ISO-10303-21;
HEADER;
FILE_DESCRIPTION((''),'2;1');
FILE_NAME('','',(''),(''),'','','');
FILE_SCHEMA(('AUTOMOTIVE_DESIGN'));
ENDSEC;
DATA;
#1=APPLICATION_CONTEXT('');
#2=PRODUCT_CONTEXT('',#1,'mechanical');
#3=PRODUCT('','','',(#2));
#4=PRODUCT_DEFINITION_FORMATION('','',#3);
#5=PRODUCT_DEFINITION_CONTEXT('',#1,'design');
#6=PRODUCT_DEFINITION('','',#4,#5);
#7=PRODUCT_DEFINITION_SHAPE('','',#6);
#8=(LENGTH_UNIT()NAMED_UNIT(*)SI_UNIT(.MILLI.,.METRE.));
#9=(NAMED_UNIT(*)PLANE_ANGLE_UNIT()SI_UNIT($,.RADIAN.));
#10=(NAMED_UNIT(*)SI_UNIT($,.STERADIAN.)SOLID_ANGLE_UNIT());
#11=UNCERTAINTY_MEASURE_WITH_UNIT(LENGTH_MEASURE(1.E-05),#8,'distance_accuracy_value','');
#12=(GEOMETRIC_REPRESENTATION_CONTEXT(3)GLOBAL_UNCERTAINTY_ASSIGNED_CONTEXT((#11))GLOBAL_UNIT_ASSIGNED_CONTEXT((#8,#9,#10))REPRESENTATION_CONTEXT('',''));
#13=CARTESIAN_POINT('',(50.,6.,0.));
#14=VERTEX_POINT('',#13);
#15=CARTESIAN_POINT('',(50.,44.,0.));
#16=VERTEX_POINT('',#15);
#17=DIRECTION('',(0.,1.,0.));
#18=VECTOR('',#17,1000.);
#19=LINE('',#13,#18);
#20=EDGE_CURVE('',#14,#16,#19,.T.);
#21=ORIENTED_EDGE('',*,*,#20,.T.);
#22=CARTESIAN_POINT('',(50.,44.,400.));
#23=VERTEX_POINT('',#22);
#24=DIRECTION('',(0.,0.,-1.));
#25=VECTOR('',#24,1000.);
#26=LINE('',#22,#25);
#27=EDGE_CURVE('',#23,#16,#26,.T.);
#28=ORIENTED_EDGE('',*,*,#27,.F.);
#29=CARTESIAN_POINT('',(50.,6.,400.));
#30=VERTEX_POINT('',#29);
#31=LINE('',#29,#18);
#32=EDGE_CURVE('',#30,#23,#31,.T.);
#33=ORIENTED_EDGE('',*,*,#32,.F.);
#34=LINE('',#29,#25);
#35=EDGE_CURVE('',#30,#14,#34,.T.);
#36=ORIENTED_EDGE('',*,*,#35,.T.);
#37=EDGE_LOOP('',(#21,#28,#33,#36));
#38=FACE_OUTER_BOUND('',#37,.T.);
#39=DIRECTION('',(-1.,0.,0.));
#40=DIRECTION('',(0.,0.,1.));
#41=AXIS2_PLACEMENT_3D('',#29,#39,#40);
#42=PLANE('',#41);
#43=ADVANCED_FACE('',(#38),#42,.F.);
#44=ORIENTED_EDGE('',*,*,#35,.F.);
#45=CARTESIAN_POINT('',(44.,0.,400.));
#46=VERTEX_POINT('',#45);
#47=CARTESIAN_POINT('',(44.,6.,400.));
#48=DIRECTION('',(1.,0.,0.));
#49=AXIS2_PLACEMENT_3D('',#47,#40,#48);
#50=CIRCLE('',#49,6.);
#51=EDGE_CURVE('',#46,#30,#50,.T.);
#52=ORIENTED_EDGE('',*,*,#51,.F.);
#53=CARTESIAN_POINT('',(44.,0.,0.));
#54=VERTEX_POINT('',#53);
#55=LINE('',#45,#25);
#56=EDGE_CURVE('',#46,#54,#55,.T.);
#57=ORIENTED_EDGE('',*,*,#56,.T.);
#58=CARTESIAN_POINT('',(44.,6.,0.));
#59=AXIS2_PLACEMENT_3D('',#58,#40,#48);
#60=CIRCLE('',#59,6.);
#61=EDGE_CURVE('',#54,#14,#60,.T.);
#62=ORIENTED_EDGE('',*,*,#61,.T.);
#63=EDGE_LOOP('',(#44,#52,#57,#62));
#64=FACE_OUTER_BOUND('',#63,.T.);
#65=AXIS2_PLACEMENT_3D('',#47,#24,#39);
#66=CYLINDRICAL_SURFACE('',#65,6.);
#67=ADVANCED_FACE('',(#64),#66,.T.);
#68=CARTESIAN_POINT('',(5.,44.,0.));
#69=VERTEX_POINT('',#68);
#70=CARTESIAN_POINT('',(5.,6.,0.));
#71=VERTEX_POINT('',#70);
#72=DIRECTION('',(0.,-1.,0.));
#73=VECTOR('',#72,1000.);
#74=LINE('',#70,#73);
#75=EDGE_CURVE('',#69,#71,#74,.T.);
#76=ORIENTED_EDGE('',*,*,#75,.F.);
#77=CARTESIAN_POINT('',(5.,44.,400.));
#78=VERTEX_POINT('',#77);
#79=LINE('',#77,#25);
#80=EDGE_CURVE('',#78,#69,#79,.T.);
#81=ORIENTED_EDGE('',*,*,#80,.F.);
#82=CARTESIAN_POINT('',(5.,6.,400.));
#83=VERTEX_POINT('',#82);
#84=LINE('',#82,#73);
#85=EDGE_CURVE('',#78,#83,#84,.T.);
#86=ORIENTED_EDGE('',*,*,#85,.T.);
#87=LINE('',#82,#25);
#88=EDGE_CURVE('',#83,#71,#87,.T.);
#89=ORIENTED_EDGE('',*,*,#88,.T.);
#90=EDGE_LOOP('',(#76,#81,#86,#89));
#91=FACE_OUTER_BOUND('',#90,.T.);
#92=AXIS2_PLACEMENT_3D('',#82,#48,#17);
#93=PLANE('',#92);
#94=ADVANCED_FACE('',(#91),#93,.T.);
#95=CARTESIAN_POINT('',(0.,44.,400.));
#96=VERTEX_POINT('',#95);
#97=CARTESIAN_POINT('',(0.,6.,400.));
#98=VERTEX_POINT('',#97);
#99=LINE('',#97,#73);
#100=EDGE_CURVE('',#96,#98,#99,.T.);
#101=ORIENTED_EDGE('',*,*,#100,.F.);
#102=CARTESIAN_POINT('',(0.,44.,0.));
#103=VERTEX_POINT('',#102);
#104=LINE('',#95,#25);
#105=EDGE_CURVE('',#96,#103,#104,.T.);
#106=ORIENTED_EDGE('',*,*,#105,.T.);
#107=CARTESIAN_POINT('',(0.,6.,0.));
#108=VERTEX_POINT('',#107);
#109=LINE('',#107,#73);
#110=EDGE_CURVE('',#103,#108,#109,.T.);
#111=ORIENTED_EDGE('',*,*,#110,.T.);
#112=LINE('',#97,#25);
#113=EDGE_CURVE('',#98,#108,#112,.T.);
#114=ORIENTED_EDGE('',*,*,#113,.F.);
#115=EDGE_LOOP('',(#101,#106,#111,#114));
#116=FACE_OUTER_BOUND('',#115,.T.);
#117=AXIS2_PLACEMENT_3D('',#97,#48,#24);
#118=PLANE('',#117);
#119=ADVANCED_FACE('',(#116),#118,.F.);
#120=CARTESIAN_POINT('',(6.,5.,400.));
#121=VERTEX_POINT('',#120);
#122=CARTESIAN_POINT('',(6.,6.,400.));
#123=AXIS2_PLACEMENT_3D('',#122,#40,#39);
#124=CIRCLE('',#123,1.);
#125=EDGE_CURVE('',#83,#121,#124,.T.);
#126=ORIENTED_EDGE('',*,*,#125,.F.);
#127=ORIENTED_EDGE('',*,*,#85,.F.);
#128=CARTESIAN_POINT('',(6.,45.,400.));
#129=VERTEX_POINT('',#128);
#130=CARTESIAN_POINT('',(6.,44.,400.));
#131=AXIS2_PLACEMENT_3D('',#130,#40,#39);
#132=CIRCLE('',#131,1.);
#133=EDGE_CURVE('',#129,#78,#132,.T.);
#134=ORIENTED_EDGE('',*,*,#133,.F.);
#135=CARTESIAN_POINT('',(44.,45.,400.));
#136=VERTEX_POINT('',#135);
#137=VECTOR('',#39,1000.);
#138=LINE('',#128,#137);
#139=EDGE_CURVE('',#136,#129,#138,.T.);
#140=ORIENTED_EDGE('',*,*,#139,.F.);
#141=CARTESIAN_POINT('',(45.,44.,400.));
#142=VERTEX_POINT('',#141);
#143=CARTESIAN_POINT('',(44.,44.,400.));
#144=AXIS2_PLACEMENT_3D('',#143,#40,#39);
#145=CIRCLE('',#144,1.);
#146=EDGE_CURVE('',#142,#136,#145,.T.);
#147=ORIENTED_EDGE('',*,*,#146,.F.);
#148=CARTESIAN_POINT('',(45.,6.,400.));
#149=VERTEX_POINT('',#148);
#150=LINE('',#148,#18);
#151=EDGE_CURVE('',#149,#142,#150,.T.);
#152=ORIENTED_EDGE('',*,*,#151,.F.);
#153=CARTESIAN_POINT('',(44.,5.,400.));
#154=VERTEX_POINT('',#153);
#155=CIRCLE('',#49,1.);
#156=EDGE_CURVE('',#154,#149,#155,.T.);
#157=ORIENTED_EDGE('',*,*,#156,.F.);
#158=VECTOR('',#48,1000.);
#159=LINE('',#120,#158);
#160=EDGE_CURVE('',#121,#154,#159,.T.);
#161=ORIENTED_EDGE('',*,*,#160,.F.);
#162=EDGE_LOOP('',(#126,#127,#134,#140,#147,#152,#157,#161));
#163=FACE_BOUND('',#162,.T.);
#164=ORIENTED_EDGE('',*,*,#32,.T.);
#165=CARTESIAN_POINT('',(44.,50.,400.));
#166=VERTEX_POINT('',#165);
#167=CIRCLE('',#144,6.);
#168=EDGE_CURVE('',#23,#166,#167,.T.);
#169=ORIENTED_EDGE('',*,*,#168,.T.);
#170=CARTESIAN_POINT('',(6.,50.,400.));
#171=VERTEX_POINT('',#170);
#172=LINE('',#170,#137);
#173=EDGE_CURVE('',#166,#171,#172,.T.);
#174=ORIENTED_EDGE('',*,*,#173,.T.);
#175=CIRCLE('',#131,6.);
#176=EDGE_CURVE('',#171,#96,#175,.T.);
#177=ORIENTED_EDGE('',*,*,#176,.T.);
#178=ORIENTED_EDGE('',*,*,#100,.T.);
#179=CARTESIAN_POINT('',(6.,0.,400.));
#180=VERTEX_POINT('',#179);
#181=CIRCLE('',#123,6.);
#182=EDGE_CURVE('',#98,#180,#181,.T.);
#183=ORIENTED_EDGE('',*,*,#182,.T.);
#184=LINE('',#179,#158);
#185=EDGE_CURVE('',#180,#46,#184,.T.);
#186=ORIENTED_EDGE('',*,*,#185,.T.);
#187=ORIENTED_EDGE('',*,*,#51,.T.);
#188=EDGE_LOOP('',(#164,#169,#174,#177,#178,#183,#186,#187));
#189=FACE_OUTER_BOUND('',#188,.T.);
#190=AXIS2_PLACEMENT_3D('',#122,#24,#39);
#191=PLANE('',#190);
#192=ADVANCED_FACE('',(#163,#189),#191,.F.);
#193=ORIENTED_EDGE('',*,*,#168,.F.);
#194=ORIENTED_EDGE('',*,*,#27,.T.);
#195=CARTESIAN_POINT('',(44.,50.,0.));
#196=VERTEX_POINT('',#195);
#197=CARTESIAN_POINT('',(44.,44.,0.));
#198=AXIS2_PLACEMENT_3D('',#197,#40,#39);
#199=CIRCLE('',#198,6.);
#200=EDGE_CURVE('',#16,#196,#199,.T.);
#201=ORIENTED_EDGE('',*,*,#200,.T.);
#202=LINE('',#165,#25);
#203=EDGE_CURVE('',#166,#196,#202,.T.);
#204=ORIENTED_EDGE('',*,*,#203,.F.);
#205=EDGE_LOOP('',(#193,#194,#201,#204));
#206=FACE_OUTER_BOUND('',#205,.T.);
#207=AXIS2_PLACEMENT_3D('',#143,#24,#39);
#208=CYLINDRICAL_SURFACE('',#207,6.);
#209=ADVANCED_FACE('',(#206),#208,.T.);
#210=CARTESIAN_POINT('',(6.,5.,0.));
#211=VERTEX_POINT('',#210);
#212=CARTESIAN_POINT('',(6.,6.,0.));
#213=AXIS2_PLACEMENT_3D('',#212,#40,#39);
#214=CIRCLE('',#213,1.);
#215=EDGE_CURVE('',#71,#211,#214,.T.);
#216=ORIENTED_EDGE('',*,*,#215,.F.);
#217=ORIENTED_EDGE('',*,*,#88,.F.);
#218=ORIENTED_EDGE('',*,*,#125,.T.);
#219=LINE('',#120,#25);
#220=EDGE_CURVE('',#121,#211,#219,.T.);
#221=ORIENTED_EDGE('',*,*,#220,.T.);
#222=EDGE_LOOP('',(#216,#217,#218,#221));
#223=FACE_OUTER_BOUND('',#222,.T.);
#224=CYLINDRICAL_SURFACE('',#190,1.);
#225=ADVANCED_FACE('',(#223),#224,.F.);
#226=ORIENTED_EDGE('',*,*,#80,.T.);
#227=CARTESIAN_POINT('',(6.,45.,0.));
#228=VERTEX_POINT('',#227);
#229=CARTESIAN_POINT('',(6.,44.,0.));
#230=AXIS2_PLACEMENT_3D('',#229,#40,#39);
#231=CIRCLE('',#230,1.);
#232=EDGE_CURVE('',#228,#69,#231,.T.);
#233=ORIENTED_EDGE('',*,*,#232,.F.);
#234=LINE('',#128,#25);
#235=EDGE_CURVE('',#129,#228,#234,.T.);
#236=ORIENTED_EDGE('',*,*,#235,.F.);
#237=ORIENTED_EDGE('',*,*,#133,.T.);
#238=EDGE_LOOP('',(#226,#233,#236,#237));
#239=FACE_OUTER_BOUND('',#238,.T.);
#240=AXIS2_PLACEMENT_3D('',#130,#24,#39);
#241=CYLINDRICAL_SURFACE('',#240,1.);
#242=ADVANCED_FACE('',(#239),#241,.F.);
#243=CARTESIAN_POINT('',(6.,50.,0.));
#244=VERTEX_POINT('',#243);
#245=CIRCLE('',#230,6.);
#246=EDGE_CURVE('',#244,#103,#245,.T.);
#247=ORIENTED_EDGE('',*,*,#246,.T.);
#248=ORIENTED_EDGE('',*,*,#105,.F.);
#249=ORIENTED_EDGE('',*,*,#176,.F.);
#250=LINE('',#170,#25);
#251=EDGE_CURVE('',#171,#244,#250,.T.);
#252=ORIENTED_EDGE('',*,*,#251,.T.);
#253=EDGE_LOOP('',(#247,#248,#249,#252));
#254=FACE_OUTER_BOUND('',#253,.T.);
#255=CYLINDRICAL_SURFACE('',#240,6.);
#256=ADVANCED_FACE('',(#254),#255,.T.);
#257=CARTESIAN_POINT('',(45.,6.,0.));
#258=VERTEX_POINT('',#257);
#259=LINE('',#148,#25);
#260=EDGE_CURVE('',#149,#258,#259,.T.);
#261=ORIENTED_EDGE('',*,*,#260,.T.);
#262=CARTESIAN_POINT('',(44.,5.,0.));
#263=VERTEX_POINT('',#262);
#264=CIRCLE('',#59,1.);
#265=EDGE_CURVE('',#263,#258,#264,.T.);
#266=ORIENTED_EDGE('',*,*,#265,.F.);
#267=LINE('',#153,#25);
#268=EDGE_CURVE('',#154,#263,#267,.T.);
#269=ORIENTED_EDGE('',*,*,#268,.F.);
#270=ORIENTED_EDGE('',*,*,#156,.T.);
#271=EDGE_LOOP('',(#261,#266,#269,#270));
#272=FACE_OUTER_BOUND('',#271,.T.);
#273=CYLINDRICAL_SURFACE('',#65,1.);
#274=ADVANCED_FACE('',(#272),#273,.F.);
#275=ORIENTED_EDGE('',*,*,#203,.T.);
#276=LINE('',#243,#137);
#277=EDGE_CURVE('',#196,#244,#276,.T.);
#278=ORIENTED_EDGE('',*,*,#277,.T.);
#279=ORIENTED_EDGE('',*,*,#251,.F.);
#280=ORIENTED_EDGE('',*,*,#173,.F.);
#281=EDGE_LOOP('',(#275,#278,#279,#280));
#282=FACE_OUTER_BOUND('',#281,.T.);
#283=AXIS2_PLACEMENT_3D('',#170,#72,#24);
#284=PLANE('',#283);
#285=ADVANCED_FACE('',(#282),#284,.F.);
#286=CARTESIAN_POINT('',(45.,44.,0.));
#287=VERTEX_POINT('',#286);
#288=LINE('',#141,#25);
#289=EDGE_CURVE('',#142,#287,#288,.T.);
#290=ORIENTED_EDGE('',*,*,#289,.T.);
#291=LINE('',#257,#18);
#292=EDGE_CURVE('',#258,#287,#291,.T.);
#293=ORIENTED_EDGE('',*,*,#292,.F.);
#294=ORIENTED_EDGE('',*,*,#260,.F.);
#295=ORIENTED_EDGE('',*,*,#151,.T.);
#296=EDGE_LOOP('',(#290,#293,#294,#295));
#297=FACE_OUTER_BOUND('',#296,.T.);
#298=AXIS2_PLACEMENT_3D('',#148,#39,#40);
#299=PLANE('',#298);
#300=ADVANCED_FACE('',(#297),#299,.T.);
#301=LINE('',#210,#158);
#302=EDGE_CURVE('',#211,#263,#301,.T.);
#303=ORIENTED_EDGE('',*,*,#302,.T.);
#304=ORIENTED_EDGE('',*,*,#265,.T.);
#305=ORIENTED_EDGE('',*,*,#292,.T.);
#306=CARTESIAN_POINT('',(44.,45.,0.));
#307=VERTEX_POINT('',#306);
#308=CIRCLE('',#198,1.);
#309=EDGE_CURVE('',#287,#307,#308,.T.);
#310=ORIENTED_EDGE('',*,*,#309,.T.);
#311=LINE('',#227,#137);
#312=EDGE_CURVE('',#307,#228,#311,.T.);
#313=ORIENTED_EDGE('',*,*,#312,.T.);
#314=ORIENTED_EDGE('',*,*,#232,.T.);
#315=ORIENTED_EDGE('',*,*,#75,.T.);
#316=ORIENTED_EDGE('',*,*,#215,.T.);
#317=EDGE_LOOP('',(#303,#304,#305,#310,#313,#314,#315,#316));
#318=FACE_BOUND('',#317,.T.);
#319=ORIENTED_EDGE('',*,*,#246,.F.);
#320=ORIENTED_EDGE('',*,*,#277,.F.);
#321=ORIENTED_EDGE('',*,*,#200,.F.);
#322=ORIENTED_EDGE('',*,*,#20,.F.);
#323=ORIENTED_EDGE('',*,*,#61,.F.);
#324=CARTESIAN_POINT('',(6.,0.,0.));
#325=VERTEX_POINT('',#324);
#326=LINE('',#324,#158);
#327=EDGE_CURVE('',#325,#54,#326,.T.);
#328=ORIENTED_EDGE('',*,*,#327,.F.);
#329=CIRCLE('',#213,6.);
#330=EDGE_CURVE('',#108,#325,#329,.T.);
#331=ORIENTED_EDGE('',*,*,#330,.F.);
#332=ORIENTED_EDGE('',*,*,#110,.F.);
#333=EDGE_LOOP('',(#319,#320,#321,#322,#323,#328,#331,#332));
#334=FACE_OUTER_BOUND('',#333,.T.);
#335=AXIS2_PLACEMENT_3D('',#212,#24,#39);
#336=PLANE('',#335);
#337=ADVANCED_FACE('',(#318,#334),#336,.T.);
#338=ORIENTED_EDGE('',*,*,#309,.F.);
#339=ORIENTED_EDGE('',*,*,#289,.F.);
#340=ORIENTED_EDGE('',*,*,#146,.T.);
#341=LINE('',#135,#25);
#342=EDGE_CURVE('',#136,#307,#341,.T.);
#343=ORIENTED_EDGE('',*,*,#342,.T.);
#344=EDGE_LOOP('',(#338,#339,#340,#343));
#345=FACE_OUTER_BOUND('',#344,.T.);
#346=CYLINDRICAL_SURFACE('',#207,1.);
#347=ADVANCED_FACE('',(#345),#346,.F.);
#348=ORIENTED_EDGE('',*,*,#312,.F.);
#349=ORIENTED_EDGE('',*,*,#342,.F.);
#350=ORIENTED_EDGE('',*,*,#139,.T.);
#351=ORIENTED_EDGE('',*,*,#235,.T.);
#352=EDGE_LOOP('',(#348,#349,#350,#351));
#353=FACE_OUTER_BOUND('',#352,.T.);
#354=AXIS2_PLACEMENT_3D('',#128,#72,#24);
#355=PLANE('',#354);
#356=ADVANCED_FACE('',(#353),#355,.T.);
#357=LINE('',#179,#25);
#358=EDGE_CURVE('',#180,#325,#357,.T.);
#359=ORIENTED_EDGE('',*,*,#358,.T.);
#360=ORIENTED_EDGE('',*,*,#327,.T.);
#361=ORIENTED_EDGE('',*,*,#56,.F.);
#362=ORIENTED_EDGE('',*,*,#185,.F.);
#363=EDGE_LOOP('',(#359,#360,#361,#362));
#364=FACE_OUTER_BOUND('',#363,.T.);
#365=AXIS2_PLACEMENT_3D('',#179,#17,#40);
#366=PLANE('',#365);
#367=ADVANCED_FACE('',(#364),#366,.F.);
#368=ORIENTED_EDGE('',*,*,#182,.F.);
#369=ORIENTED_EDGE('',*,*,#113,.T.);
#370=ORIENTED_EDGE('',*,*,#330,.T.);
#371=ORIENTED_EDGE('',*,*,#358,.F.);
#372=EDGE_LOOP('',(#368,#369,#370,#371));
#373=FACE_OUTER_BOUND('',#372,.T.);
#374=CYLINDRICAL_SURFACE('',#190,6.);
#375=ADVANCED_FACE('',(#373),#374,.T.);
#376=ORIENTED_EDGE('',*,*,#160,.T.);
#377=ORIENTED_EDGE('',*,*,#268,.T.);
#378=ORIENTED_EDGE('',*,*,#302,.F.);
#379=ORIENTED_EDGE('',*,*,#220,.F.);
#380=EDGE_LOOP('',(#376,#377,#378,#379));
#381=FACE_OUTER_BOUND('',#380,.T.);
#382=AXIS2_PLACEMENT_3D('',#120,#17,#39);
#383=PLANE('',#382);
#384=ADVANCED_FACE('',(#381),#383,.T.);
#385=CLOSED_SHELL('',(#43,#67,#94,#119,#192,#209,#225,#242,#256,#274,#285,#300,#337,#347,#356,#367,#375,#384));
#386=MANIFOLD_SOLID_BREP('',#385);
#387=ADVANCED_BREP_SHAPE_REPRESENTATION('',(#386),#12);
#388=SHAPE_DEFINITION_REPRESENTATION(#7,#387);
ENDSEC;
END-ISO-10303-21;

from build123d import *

# Parameters (mm, degrees)
BOSS_EXTRUDE1_DEPTH = 400


with BuildPart() as part:
    # Sketch1 → Boss-Extrude1 (new body)
    with BuildSketch(Plane.XY):
        with BuildLine():
            Line((6, 0), (44, 0))
            ThreePointArc((44, 0), (48.242640687, 1.757359313), (50, 6))
            Line((50, 6), (50, 44))
            ThreePointArc((50, 44), (48.242640687, 48.242640687), (44, 50))
            Line((44, 50), (6, 50))
            ThreePointArc((6, 50), (1.757359313, 48.242640687), (0, 44))
            Line((0, 44), (0, 6))
            ThreePointArc((0, 6), (1.757359313, 1.757359313), (6, 0))
        make_face()
        with BuildLine():
            Line((6, 45), (44, 45))
            ThreePointArc((44, 45), (44.707106781, 44.707106781), (45, 44))
            Line((45, 44), (45, 6))
            ThreePointArc((45, 6), (44.707106781, 5.292893219), (44, 5))
            Line((44, 5), (6, 5))
            ThreePointArc((6, 5), (5.292893219, 5.292893219), (5, 6))
            Line((5, 6), (5, 44))
            ThreePointArc((5, 44), (5.292893219, 44.707106781), (6, 45))
        make_face(mode=Mode.SUBTRACT)
    extrude(amount=BOSS_EXTRUDE1_DEPTH)


solid = part.part
